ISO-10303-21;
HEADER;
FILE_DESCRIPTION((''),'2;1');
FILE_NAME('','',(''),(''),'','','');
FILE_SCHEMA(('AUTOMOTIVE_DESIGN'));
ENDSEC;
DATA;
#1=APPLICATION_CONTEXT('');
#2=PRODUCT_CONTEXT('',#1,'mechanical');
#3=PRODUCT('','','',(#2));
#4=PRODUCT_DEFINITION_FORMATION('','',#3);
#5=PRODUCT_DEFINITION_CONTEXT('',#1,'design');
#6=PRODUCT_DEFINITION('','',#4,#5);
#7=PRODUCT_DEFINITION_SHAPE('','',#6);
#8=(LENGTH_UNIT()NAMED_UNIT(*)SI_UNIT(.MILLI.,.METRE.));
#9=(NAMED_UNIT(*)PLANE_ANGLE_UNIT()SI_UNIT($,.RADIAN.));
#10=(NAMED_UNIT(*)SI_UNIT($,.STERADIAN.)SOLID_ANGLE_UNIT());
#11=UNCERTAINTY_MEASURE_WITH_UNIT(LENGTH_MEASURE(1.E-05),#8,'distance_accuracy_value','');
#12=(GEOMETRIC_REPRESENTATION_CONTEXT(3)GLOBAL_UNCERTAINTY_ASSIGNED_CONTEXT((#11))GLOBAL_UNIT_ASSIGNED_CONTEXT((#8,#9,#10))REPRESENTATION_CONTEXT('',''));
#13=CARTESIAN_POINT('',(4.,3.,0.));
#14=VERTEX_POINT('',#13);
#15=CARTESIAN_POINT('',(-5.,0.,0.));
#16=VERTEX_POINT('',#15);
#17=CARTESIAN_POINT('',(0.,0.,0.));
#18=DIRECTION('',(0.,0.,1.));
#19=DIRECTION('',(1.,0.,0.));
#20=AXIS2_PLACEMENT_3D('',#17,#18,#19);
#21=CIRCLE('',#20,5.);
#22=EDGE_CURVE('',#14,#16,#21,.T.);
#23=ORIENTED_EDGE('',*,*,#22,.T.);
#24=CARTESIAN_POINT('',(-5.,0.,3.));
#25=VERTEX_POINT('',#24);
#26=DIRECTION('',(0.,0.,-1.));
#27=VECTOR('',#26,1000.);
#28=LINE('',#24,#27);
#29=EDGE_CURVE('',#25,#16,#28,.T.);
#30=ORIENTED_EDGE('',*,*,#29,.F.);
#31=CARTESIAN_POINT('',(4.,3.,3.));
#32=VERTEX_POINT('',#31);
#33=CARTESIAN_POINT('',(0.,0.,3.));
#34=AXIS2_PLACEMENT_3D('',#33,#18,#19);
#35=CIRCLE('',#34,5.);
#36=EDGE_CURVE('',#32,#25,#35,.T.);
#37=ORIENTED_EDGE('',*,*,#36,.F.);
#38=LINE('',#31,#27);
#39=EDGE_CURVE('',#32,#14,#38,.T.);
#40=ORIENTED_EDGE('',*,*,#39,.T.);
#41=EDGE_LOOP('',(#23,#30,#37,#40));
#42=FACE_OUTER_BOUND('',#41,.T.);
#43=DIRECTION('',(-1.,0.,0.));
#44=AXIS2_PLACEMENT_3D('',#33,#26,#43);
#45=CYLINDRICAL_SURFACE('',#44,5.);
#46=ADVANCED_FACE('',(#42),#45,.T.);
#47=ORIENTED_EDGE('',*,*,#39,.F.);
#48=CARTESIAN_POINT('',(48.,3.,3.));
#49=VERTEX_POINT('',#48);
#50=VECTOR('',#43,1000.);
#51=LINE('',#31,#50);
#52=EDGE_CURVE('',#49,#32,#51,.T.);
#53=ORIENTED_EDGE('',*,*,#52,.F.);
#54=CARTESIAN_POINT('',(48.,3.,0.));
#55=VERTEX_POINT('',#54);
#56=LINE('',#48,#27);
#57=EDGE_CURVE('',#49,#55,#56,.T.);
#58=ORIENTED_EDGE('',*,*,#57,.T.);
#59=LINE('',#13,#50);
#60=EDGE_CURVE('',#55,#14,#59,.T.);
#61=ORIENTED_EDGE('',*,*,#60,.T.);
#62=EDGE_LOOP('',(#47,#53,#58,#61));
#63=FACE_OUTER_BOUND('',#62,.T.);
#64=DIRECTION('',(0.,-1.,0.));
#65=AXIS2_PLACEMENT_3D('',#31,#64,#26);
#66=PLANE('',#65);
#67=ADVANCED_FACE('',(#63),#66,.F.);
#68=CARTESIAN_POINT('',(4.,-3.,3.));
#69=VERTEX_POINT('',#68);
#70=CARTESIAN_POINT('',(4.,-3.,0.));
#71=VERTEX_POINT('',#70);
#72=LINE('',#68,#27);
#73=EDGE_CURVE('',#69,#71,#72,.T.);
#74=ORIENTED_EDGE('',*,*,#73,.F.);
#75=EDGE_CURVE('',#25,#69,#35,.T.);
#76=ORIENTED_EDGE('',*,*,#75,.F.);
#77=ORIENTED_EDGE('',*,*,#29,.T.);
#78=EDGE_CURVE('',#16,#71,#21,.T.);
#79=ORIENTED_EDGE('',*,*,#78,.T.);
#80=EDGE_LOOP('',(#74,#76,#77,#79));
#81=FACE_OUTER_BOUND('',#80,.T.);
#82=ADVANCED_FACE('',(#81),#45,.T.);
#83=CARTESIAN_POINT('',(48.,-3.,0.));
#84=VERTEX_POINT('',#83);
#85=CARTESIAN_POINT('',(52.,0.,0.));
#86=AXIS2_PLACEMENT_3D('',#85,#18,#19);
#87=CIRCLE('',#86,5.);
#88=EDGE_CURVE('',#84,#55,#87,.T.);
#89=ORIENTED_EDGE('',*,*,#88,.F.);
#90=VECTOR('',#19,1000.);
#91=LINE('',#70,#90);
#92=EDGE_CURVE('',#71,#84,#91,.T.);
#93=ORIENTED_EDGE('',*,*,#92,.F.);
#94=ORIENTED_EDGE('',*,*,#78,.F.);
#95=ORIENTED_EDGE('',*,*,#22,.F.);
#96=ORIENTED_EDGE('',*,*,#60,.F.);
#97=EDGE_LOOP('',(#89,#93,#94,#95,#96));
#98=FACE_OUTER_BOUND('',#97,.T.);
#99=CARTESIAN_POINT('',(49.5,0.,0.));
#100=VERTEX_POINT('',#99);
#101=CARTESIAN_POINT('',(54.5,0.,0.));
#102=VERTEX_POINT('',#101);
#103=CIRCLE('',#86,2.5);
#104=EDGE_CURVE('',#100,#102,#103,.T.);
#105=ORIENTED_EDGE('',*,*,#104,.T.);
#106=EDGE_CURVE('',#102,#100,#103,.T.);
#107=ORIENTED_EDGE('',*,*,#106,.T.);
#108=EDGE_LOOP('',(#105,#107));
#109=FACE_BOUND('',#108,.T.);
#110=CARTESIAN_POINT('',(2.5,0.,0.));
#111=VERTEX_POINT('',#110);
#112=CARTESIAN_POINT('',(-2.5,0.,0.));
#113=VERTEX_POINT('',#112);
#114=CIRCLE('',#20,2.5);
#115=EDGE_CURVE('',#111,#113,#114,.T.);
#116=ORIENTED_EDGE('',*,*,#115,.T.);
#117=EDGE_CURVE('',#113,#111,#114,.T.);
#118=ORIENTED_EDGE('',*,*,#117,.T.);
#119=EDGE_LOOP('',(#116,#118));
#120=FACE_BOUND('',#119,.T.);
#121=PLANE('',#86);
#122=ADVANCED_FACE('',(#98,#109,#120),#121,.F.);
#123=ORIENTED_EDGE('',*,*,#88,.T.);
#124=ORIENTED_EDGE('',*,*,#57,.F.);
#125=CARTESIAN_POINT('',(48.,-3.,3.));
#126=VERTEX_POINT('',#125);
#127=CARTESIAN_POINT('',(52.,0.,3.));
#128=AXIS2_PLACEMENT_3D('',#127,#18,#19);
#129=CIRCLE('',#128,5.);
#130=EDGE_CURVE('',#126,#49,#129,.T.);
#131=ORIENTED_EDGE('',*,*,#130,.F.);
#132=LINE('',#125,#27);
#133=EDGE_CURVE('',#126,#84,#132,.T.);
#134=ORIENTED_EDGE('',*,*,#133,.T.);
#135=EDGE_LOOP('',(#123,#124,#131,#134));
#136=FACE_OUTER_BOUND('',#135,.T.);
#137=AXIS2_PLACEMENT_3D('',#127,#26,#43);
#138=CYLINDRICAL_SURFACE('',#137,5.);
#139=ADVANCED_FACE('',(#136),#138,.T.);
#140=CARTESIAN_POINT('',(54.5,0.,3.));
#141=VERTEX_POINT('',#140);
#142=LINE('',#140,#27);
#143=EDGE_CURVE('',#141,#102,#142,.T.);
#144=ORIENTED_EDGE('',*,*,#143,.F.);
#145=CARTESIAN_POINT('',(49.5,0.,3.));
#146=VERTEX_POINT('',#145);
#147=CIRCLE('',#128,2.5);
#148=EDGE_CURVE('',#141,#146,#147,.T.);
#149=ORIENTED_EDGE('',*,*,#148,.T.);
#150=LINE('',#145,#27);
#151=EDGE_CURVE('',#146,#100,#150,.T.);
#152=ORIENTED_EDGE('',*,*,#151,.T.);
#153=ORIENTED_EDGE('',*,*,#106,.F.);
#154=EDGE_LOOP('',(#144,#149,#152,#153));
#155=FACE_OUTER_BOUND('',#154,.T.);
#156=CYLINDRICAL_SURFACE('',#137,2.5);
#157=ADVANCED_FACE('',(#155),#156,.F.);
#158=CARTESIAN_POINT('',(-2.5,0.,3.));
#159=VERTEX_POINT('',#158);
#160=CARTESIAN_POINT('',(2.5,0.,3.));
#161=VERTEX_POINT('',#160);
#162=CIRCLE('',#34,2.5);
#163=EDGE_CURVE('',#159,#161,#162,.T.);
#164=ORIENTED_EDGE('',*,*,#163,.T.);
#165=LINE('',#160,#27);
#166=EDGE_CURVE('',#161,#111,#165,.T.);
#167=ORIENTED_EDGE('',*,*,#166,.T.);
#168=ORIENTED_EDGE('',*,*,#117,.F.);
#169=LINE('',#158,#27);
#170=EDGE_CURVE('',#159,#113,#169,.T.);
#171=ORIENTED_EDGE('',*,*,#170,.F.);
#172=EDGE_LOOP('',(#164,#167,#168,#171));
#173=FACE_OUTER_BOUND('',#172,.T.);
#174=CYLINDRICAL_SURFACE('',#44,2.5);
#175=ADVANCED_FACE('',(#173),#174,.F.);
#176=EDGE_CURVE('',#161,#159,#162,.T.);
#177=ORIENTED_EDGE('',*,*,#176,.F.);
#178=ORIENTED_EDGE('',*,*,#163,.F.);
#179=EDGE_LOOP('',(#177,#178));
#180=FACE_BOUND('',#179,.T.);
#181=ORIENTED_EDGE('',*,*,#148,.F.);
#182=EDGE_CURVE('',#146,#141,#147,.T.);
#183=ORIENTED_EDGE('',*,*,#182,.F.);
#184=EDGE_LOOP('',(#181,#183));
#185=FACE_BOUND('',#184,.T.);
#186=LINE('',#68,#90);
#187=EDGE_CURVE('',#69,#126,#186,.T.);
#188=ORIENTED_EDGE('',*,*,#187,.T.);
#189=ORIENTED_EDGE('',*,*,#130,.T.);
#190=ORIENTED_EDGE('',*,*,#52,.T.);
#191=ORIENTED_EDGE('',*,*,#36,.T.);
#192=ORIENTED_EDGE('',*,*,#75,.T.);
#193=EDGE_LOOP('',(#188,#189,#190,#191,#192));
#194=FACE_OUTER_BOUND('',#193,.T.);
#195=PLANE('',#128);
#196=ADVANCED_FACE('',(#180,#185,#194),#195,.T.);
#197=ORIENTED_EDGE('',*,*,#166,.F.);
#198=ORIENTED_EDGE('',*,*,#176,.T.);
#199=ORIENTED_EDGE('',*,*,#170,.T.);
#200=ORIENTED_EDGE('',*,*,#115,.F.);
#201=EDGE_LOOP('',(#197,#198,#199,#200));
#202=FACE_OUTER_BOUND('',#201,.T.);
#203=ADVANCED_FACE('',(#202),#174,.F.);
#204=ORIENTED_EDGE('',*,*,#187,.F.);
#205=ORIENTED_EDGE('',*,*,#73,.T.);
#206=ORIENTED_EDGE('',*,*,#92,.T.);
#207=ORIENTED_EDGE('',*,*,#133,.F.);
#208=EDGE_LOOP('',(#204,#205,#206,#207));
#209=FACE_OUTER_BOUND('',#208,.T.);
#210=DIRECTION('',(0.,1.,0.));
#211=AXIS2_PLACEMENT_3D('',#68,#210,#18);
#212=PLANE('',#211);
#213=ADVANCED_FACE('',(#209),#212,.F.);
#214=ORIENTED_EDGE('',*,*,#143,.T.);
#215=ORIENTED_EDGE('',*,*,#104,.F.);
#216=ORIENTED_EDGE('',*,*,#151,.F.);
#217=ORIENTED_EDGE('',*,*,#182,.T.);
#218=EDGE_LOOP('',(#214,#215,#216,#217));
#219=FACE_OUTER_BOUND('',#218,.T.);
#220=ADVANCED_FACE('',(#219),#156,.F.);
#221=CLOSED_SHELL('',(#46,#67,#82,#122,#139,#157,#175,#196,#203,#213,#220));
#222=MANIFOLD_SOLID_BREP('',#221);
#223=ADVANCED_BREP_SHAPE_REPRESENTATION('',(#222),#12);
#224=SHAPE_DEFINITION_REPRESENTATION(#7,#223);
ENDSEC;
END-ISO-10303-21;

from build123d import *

# Parameters (mm, degrees)
SKETCH1_R           = 2.5
BOSS_EXTRUDE1_DEPTH = 3


with BuildPart() as part:
    # Sketch1 → Boss-Extrude1 (new body)
    with BuildSketch(Plane.XY):
        with BuildLine():
            Line((4, 3), (48, 3))
            ThreePointArc((48, 3), (57, 0), (48, -3))
            Line((48, -3), (4, -3))
            ThreePointArc((4, -3), (-5, 0), (4, 3))
        make_face()
        Circle(SKETCH1_R, mode=Mode.SUBTRACT)
        with Locations((52, 0)):
            Circle(SKETCH1_R, mode=Mode.SUBTRACT)
    extrude(amount=BOSS_EXTRUDE1_DEPTH)


solid = part.part
